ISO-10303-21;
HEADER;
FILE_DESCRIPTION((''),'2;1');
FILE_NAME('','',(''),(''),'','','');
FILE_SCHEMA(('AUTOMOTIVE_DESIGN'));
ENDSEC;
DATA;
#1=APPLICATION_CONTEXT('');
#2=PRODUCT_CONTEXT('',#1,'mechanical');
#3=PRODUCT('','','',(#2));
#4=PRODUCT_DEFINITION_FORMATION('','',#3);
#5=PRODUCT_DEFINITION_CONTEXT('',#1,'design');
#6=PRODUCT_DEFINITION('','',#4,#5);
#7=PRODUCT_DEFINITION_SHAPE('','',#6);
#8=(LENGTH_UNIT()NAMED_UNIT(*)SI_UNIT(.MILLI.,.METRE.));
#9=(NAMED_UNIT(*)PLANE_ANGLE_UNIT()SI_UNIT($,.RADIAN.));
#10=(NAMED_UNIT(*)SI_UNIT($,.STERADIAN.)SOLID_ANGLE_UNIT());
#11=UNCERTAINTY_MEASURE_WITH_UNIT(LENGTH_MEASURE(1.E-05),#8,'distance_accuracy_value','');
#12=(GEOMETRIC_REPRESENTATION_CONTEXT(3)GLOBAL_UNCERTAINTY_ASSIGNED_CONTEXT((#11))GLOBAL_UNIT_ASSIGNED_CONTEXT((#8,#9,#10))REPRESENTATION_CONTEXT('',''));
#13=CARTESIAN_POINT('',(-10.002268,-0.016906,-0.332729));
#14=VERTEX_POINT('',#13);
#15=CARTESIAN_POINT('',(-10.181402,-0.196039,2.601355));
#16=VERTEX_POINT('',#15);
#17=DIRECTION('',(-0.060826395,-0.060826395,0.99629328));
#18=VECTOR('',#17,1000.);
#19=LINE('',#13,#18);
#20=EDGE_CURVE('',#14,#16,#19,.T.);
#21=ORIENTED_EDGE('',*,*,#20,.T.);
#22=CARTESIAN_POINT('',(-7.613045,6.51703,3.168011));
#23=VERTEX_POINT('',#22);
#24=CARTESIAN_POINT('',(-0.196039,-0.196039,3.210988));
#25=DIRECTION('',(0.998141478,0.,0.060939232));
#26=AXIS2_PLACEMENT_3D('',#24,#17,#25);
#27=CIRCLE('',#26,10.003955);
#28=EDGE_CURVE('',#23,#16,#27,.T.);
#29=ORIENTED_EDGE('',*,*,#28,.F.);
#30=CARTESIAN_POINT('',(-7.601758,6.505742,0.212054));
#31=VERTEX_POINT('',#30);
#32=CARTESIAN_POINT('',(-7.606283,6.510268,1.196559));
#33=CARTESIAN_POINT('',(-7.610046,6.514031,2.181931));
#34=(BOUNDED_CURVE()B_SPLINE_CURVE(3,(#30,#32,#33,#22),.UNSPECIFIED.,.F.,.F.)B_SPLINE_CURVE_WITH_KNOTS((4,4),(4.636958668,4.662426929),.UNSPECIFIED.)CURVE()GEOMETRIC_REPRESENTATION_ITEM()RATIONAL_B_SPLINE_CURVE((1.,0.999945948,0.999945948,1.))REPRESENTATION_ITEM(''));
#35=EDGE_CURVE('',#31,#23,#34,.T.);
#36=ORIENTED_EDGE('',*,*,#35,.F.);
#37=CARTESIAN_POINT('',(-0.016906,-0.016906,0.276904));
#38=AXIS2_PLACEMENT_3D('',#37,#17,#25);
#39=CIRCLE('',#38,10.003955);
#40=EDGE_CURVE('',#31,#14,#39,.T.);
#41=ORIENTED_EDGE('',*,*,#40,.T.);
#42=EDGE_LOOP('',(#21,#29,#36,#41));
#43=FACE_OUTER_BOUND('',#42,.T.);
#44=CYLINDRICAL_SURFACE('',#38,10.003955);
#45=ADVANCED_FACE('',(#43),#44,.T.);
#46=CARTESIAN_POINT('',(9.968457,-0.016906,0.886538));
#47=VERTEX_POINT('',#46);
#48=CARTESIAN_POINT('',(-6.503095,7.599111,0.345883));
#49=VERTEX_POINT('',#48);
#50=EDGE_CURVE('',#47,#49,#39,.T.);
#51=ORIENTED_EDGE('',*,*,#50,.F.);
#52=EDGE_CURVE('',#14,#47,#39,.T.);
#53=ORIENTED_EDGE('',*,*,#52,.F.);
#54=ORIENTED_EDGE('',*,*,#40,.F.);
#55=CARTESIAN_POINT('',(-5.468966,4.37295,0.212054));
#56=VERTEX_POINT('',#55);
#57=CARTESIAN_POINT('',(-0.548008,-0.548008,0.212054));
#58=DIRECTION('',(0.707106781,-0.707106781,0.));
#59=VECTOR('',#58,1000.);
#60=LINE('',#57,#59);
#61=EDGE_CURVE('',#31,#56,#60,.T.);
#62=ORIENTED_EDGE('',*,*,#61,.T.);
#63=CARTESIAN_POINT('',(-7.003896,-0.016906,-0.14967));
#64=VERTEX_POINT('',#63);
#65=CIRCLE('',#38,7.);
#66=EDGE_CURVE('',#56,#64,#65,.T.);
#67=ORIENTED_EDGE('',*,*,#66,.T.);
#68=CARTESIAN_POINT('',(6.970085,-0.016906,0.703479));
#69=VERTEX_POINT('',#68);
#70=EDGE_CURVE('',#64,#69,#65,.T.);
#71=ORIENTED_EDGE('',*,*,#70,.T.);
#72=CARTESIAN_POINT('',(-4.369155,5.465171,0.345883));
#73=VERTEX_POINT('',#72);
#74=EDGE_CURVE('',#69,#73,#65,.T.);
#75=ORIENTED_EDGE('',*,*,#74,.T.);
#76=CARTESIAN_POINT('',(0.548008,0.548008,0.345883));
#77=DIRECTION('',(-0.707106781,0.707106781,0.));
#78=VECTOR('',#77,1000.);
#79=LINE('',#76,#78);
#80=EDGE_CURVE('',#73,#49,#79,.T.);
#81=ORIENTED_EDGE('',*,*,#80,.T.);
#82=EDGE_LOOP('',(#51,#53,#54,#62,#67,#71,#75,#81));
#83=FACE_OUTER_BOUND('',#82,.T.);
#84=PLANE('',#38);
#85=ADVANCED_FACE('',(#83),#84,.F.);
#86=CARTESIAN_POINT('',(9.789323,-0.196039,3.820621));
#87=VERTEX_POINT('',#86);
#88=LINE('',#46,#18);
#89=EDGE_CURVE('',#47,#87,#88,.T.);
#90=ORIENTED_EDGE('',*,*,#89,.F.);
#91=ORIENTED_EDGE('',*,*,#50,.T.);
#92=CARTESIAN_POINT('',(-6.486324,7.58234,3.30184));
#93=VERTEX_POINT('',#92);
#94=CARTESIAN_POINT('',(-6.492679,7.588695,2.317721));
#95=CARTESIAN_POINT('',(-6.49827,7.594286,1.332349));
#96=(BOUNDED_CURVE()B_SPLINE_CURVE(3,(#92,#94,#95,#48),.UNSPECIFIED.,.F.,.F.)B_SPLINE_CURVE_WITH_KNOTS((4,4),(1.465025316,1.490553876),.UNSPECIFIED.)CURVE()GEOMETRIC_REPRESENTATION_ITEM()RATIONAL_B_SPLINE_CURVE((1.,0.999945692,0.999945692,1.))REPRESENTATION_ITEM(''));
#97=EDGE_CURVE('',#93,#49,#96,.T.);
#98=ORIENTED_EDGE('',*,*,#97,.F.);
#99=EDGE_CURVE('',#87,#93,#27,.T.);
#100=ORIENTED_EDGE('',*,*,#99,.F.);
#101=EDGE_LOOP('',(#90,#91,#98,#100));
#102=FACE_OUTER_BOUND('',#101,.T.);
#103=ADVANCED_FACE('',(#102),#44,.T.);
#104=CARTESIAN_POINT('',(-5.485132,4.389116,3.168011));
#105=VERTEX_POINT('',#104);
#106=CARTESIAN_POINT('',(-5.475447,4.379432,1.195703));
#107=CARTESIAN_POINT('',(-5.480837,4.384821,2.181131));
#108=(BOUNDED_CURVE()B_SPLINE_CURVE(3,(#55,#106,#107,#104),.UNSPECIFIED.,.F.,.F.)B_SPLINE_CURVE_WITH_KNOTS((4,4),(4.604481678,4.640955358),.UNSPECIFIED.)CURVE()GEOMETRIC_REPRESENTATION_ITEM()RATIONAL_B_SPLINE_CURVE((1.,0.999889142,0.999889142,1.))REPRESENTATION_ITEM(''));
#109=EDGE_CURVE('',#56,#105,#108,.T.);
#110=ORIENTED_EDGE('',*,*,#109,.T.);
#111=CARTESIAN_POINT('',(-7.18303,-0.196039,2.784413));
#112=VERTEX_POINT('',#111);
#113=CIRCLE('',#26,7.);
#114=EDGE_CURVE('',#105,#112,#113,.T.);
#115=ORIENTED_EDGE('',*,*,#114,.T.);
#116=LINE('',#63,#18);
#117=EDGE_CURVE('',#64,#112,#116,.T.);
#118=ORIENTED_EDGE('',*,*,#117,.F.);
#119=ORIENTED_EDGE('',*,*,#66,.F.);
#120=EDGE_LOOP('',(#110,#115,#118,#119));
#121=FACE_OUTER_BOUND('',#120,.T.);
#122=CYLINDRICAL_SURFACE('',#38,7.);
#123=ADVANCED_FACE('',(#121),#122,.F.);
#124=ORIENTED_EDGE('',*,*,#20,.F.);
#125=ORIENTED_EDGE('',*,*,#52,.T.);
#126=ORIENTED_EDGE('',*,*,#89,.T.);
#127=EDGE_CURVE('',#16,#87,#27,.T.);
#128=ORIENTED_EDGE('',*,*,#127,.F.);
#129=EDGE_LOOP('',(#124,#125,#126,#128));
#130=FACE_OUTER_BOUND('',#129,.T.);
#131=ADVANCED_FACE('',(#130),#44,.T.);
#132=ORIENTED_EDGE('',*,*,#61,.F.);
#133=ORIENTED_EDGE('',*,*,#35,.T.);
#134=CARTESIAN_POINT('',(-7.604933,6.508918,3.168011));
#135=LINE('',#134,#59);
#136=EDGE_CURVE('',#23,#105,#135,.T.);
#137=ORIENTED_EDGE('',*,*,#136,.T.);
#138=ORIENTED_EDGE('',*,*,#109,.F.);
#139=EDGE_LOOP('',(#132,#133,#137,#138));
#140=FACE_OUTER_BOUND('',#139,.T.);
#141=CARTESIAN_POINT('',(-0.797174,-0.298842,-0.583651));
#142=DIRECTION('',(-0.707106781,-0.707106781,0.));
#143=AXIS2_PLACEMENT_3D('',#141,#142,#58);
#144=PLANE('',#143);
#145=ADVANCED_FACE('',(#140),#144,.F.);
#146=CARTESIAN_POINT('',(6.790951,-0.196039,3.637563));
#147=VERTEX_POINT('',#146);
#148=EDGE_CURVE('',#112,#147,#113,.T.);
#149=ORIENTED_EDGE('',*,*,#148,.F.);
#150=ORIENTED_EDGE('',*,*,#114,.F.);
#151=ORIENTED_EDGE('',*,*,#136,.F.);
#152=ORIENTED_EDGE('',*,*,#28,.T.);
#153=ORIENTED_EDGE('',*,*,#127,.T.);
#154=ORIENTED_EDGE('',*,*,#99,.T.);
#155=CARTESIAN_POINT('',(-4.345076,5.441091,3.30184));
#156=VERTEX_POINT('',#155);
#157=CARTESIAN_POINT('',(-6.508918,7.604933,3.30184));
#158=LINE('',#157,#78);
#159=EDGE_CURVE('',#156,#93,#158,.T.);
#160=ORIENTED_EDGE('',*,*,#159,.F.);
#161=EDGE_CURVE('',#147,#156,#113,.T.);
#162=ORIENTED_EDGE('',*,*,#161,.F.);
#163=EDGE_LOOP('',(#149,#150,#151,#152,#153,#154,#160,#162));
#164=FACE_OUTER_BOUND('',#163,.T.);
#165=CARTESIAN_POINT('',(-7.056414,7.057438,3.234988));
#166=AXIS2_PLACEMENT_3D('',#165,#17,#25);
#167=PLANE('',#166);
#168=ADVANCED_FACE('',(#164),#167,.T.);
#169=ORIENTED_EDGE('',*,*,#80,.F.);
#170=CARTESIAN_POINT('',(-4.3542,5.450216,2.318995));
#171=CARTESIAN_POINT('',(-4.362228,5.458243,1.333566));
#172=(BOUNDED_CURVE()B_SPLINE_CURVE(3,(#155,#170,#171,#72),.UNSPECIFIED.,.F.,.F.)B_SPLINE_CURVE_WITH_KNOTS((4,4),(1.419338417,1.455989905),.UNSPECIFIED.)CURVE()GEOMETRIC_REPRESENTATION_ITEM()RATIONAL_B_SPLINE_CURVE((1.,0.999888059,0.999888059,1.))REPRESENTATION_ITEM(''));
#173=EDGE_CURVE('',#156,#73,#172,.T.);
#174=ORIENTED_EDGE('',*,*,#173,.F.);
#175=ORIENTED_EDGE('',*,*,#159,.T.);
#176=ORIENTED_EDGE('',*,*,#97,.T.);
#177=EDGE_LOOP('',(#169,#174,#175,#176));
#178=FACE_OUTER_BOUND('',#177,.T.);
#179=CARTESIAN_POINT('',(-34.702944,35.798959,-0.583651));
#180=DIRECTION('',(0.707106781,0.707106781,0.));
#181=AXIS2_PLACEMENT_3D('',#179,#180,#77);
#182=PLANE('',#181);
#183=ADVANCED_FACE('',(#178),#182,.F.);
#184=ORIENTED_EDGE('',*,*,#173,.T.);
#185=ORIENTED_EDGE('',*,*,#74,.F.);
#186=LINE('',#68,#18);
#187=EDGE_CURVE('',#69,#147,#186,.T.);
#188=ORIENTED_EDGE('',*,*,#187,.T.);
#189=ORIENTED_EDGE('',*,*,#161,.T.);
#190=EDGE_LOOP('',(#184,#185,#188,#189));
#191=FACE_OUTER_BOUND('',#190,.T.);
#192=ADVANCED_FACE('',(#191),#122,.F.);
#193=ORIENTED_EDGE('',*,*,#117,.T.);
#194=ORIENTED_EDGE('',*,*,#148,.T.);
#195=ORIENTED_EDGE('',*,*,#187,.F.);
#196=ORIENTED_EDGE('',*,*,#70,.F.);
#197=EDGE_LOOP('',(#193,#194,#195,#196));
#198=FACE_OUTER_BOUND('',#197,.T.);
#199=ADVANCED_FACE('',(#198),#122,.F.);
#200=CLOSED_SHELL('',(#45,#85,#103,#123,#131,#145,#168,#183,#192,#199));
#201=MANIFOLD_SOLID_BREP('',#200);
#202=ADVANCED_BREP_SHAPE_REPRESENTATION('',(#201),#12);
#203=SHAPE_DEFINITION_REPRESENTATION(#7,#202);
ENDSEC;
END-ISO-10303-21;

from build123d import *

# Parameters (mm, degrees)
BASE_EXTRUDE_DEPTH      = 0.001
BASE_EXTRUDE_DEPTH_BACK = 0.001
SKETCH6_W               = 2.905
SKETCH6_H               = 3.96
SKETCH8_R               = 10.003955179
SKETCH8_R_2             = 7
BOSS_EXTRUDE1_DEPTH     = 2.945
CUT_EXTRUDE1_DEPTH      = 15.963360846
CUT_EXTRUDE1_DEPTH_BACK = 15.963360846


with BuildPart() as part:
    # Sketch6 → Base-Extrude (new, two sides: drawn at the far end of the back side and taken through both)
    with BuildSketch(Plane(origin=(-4.242640687, 4.242640687, 3.255), x_dir=(0.060826394912022484, 0.060826394912020985, -0.9962932797946665), z_dir=(0.7044857341934017, 0.7044857341933883, 0.08602151263484296)).offset(-BASE_EXTRUDE_DEPTH_BACK)):
        with Locations((1.4725, 2)):
            Rectangle(SKETCH6_W, SKETCH6_H)
    extrude(amount=BASE_EXTRUDE_DEPTH + BASE_EXTRUDE_DEPTH_BACK)

    # Sketch8 → Boss-Extrude1 (add)
    with BuildSketch(Plane(origin=(-0.196039494, -0.196039494, 3.210988109), x_dir=(0.9981483386916642, -0.003915635910269119, 0.06070059112141398), z_dir=(-0.060826394912022415, -0.0608263949120211, 0.9962932797946664))):
        with Locations(Location((0, 0, 0), (0, 0, 0.224766173))):
            Circle(SKETCH8_R)
        with Locations(Location((0, 0, 0), (0, 0, 0.224766173))):
            Circle(SKETCH8_R_2, mode=Mode.SUBTRACT)
    extrude(amount=-BOSS_EXTRUDE1_DEPTH)

    # Sketch9 → Cut-Extrude1 (cut, two sides: drawn at the far end of the back side and taken through both)
    with BuildSketch(Plane.XY.offset(-CUT_EXTRUDE1_DEPTH_BACK)):
        Polygon((-34.702943681, 35.798959192), (0.298841987, 0.797173523), (-0.797173523, -0.298841987), (-36.894974703, 35.798959192), align=None)
    extrude(amount=CUT_EXTRUDE1_DEPTH + CUT_EXTRUDE1_DEPTH_BACK, mode=Mode.SUBTRACT)


solid = part.part
